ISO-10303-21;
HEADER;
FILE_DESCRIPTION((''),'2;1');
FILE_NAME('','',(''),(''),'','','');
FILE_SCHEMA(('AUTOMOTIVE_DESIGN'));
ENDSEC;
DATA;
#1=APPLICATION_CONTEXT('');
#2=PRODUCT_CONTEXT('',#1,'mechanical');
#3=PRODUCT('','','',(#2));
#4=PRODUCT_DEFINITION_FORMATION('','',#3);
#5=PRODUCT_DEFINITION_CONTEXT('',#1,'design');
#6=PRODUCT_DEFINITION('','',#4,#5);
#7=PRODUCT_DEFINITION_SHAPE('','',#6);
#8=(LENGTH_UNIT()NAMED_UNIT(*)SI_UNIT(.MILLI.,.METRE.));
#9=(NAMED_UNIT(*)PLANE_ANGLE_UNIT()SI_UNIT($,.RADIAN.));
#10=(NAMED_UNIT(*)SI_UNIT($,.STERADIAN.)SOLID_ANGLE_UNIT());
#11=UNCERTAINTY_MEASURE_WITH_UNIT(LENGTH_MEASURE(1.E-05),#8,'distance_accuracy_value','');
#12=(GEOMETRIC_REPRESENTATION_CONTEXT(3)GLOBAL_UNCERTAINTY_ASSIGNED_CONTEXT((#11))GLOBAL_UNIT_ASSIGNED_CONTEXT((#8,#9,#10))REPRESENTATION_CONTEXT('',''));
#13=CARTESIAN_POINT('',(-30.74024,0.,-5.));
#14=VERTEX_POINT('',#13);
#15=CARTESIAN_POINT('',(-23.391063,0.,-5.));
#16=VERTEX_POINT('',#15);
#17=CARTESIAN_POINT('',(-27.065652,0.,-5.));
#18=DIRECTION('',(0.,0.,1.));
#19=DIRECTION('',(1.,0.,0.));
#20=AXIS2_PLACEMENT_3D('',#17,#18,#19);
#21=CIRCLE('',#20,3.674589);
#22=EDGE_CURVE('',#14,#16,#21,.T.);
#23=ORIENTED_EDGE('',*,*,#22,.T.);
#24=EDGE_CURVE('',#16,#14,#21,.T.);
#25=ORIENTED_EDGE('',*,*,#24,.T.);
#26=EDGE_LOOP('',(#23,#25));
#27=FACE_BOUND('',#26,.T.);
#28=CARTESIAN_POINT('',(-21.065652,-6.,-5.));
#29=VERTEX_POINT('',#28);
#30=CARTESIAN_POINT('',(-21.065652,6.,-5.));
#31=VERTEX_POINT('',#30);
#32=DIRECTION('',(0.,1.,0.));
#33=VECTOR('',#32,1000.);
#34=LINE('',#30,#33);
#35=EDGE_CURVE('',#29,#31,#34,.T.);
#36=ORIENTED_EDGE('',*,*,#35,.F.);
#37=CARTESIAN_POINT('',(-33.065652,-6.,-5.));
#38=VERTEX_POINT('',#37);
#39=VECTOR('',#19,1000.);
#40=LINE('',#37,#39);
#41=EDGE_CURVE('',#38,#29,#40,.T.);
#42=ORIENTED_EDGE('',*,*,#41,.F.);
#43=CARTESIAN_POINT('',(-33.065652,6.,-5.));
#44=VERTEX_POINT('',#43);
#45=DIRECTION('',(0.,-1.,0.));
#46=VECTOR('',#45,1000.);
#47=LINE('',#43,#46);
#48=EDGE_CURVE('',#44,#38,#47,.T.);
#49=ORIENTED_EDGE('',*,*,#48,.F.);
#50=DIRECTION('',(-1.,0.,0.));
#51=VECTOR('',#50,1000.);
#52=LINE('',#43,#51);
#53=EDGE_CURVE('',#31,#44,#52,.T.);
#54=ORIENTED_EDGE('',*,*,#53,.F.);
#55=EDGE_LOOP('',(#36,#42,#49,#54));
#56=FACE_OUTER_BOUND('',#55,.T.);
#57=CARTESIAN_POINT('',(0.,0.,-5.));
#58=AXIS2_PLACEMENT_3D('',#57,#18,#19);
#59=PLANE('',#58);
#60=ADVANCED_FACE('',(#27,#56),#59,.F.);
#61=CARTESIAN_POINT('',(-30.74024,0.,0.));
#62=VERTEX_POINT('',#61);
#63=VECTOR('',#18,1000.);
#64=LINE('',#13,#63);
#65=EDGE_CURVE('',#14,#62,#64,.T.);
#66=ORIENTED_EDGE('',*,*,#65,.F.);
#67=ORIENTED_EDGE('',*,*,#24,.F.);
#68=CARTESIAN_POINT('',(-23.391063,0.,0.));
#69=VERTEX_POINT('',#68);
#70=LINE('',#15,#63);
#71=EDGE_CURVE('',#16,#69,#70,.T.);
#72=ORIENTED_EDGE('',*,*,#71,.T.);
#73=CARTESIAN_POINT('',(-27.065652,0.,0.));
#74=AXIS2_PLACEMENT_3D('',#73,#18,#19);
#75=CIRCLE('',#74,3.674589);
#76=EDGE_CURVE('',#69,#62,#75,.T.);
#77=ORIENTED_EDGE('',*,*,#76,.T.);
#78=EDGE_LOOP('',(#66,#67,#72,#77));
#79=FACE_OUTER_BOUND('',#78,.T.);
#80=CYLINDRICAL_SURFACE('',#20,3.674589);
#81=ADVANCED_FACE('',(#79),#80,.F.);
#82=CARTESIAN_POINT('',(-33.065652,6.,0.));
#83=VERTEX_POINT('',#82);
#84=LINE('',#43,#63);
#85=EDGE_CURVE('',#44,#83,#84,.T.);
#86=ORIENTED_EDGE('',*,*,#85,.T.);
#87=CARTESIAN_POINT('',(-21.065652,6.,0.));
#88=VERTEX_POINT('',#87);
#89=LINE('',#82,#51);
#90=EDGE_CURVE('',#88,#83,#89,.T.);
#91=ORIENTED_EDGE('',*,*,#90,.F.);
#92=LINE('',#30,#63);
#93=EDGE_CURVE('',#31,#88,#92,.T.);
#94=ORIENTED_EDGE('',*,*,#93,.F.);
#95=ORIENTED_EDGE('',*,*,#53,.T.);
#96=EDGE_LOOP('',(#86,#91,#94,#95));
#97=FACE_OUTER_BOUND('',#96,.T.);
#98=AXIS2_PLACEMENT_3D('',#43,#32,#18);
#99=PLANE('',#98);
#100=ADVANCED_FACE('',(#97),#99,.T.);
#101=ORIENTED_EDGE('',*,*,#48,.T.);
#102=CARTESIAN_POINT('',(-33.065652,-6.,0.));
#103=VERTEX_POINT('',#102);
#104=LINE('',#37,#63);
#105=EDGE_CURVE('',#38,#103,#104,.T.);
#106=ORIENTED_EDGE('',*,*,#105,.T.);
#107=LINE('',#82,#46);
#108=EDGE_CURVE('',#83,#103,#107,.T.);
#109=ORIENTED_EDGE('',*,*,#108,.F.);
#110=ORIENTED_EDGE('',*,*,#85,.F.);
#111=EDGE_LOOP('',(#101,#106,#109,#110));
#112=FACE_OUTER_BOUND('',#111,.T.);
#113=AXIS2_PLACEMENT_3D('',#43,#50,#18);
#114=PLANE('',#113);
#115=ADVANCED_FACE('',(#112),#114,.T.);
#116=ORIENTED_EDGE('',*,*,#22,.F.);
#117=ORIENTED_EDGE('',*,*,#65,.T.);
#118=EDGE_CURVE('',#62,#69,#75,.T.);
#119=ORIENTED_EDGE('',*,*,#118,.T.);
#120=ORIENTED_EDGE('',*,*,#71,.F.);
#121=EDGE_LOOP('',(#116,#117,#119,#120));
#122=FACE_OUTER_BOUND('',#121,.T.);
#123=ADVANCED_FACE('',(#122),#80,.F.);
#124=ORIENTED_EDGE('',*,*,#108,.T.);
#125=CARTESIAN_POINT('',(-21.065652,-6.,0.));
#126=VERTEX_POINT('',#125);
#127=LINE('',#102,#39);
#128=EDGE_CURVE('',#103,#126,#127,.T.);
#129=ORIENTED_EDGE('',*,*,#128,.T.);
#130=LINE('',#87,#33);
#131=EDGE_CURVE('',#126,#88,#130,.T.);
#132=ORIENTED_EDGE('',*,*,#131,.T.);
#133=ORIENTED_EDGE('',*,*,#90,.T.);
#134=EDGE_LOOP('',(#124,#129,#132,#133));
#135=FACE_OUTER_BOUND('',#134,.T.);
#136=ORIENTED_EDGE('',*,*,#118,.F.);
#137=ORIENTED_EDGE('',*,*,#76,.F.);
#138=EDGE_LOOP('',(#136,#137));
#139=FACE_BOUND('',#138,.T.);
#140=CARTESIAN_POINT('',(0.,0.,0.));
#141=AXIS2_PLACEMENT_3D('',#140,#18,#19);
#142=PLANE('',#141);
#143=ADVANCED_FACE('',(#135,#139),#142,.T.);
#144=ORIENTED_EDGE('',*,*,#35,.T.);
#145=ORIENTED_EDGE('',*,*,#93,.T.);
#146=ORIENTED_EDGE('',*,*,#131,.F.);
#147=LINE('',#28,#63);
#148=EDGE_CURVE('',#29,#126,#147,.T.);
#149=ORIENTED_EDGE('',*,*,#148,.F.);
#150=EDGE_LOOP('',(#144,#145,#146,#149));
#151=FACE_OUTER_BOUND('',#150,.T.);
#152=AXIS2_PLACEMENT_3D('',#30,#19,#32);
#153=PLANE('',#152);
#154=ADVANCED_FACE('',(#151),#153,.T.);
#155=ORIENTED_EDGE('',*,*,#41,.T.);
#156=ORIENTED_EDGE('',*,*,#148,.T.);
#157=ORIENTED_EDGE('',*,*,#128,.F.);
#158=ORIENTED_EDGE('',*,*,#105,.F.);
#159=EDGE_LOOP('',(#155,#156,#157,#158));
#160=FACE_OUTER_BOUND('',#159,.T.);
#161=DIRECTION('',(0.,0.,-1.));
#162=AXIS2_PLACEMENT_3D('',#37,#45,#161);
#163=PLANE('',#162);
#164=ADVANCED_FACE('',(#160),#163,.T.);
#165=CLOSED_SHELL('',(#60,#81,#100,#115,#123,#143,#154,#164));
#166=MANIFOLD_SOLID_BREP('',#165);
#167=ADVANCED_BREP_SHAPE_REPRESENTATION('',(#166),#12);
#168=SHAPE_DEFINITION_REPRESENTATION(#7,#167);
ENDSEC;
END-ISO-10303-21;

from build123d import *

# Parameters (mm, degrees)
SKETCH1_W           = 12
SKETCH1_H           = 12
SKETCH1_R           = 3.674588618
BOSS_EXTRUDE1_DEPTH = 5


with BuildPart() as part:
    # Sketch1 → Boss-Extrude1 (new body)
    with BuildSketch(Plane.XY):
        with Locations((-27.065651732, 0)):
            Rectangle(SKETCH1_W, SKETCH1_H)
        with Locations((-27.065651732, 0)):
            Circle(SKETCH1_R, mode=Mode.SUBTRACT)
    extrude(amount=-BOSS_EXTRUDE1_DEPTH)


solid = part.part
